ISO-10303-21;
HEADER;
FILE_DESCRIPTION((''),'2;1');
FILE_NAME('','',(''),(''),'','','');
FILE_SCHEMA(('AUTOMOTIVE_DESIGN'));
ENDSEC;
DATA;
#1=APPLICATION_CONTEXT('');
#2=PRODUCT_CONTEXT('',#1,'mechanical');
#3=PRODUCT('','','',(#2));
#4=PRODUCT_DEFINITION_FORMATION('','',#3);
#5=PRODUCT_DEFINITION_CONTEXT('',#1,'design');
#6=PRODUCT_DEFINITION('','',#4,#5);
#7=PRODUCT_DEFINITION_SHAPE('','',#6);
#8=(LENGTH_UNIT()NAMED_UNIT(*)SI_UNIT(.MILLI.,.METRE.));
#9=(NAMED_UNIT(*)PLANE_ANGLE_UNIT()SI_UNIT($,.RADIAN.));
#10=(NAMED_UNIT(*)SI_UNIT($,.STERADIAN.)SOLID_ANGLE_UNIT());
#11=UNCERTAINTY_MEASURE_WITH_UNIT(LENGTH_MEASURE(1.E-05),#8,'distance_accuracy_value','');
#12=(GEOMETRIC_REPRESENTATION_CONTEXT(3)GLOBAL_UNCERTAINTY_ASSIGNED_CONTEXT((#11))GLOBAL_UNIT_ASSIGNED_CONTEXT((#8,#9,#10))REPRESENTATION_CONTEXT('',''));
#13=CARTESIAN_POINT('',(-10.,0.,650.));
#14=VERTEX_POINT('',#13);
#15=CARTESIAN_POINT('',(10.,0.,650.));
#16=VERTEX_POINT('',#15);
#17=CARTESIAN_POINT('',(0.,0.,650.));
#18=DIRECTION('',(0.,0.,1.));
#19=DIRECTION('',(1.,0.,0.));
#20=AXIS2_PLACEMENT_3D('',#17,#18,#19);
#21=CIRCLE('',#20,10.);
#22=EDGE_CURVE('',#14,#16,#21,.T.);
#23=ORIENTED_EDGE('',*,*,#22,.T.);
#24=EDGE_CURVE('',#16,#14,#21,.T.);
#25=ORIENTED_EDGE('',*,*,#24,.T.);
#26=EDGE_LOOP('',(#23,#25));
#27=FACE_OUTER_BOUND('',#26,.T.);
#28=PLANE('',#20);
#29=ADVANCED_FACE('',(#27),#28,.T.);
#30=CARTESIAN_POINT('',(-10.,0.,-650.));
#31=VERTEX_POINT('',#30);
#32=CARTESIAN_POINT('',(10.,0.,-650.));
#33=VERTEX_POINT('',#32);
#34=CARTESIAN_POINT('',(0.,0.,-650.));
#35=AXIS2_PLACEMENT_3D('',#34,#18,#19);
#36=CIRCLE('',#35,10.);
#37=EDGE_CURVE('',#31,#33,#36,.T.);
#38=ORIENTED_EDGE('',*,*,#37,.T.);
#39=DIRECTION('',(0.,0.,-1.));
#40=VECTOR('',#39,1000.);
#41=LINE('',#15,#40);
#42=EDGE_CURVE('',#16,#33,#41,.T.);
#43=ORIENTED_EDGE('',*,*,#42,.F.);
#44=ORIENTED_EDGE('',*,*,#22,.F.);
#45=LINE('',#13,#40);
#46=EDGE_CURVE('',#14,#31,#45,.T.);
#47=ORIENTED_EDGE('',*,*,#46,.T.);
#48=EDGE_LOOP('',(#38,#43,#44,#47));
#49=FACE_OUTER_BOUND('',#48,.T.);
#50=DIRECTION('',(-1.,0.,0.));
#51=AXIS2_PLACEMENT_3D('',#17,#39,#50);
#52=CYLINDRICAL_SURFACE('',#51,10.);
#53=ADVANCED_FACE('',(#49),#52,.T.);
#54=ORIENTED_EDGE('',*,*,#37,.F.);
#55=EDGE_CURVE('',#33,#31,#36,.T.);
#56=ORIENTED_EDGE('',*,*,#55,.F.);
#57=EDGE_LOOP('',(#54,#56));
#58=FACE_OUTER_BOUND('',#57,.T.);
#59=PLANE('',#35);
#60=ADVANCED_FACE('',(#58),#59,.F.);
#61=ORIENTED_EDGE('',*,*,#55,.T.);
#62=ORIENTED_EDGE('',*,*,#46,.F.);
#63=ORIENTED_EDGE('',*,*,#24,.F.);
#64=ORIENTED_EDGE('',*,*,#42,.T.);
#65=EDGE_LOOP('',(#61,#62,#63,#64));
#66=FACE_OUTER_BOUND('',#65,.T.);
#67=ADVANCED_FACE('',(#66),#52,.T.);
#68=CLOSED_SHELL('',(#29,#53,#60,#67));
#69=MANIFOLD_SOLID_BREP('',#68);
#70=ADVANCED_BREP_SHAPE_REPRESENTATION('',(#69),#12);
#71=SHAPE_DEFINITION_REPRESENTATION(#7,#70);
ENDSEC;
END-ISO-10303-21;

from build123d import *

# Parameters (mm, degrees)
SKETCH_1_R      = 10
EXTRUDE_1_DEPTH = 650


with BuildPart() as part:
    # 草图1 → 凸台-拉伸1 (new, symmetric)
    with BuildSketch(Plane.XY):
        Circle(SKETCH_1_R)
    extrude(amount=EXTRUDE_1_DEPTH, both=True)


solid = part.part
